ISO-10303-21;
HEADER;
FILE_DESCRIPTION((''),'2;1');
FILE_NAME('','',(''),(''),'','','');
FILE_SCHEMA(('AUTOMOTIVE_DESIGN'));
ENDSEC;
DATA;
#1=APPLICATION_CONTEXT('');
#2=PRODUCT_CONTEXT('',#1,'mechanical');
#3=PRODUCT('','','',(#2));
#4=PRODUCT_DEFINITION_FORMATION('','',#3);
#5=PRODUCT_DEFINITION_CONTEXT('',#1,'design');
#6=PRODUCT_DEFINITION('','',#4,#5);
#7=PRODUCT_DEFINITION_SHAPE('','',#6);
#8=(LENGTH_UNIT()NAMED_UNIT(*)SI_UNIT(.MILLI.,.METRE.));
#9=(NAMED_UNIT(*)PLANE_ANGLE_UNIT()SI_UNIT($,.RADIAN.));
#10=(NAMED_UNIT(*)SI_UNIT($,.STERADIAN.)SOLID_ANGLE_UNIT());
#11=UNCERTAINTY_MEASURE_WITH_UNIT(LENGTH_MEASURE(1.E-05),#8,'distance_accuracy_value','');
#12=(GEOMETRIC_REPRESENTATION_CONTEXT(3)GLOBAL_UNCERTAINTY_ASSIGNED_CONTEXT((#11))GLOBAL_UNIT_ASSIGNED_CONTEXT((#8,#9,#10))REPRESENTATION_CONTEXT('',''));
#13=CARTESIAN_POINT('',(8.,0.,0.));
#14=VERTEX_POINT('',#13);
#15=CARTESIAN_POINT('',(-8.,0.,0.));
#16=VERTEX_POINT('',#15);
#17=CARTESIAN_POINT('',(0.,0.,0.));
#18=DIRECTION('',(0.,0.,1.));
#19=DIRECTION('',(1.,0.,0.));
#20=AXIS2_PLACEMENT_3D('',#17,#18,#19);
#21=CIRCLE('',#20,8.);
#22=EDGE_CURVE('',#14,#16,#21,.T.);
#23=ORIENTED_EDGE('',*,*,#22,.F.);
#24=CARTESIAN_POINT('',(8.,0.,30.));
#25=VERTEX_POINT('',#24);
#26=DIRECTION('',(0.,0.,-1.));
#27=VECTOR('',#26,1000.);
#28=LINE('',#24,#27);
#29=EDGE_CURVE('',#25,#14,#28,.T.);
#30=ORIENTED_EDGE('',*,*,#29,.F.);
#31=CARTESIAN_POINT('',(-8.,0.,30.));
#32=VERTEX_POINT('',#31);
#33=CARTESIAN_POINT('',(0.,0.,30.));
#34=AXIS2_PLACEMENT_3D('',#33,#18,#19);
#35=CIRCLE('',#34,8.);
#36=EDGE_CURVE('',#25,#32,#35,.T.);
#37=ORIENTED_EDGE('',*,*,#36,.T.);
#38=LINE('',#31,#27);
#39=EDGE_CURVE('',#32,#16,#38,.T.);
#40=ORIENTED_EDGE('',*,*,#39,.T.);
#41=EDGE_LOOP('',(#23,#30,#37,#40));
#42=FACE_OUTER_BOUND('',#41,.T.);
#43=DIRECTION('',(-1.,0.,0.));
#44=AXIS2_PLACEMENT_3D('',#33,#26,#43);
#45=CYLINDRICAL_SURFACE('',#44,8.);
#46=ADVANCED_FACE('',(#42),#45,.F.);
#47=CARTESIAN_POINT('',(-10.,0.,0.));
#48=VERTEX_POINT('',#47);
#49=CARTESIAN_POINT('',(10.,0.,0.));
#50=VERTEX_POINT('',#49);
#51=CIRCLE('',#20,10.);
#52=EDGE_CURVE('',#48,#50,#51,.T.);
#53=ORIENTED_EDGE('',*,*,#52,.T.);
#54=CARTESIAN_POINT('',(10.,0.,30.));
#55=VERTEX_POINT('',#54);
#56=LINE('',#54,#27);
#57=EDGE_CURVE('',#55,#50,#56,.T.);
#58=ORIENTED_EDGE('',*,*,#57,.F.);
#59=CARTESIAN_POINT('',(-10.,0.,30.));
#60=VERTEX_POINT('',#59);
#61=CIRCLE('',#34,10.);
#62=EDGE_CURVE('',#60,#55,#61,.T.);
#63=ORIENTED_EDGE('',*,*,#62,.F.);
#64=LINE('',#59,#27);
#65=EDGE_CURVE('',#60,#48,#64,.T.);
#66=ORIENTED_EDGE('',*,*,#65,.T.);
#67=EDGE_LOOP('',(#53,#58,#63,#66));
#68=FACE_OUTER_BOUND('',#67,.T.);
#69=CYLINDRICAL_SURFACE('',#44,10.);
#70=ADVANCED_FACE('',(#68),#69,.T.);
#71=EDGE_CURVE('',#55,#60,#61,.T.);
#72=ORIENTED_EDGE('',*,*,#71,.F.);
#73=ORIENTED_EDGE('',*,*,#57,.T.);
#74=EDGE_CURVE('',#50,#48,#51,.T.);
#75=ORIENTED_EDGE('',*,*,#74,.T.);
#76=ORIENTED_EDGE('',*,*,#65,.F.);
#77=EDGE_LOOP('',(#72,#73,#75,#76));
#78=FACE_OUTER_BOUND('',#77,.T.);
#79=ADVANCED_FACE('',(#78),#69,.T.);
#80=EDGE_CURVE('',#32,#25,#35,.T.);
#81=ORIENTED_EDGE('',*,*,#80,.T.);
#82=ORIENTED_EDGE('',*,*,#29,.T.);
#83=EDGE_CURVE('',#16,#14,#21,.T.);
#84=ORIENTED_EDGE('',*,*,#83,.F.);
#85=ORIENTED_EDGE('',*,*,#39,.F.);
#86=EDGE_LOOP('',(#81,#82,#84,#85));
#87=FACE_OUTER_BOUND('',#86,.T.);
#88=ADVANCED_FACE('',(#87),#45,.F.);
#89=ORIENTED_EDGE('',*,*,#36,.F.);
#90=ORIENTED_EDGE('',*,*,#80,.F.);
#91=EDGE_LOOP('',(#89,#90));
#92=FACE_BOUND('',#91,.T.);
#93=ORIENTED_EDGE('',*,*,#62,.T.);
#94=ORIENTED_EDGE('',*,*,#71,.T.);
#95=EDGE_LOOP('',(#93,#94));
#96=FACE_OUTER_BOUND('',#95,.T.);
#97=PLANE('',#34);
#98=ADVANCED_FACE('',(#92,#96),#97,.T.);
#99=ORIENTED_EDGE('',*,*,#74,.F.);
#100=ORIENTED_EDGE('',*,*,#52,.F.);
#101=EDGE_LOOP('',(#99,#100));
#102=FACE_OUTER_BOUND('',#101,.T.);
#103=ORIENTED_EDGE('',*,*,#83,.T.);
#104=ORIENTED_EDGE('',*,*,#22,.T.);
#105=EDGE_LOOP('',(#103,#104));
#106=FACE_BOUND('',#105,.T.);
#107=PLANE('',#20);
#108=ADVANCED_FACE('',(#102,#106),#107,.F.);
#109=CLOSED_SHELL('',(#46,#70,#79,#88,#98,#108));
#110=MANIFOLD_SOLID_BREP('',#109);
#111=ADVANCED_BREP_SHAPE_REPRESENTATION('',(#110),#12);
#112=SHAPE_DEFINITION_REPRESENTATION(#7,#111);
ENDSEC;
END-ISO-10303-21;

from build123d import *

# Parameters (mm, degrees)
SKETCH_1_R      = 10
SKETCH_1_R_2    = 8
EXTRUDE_1_DEPTH = 30


with BuildPart() as part:
    # 草图1 → 拉伸-薄壁1 (new body)
    with BuildSketch(Plane.XY):
        Circle(SKETCH_1_R)
        Circle(SKETCH_1_R_2, mode=Mode.SUBTRACT)
    extrude(amount=EXTRUDE_1_DEPTH)


solid = part.part
